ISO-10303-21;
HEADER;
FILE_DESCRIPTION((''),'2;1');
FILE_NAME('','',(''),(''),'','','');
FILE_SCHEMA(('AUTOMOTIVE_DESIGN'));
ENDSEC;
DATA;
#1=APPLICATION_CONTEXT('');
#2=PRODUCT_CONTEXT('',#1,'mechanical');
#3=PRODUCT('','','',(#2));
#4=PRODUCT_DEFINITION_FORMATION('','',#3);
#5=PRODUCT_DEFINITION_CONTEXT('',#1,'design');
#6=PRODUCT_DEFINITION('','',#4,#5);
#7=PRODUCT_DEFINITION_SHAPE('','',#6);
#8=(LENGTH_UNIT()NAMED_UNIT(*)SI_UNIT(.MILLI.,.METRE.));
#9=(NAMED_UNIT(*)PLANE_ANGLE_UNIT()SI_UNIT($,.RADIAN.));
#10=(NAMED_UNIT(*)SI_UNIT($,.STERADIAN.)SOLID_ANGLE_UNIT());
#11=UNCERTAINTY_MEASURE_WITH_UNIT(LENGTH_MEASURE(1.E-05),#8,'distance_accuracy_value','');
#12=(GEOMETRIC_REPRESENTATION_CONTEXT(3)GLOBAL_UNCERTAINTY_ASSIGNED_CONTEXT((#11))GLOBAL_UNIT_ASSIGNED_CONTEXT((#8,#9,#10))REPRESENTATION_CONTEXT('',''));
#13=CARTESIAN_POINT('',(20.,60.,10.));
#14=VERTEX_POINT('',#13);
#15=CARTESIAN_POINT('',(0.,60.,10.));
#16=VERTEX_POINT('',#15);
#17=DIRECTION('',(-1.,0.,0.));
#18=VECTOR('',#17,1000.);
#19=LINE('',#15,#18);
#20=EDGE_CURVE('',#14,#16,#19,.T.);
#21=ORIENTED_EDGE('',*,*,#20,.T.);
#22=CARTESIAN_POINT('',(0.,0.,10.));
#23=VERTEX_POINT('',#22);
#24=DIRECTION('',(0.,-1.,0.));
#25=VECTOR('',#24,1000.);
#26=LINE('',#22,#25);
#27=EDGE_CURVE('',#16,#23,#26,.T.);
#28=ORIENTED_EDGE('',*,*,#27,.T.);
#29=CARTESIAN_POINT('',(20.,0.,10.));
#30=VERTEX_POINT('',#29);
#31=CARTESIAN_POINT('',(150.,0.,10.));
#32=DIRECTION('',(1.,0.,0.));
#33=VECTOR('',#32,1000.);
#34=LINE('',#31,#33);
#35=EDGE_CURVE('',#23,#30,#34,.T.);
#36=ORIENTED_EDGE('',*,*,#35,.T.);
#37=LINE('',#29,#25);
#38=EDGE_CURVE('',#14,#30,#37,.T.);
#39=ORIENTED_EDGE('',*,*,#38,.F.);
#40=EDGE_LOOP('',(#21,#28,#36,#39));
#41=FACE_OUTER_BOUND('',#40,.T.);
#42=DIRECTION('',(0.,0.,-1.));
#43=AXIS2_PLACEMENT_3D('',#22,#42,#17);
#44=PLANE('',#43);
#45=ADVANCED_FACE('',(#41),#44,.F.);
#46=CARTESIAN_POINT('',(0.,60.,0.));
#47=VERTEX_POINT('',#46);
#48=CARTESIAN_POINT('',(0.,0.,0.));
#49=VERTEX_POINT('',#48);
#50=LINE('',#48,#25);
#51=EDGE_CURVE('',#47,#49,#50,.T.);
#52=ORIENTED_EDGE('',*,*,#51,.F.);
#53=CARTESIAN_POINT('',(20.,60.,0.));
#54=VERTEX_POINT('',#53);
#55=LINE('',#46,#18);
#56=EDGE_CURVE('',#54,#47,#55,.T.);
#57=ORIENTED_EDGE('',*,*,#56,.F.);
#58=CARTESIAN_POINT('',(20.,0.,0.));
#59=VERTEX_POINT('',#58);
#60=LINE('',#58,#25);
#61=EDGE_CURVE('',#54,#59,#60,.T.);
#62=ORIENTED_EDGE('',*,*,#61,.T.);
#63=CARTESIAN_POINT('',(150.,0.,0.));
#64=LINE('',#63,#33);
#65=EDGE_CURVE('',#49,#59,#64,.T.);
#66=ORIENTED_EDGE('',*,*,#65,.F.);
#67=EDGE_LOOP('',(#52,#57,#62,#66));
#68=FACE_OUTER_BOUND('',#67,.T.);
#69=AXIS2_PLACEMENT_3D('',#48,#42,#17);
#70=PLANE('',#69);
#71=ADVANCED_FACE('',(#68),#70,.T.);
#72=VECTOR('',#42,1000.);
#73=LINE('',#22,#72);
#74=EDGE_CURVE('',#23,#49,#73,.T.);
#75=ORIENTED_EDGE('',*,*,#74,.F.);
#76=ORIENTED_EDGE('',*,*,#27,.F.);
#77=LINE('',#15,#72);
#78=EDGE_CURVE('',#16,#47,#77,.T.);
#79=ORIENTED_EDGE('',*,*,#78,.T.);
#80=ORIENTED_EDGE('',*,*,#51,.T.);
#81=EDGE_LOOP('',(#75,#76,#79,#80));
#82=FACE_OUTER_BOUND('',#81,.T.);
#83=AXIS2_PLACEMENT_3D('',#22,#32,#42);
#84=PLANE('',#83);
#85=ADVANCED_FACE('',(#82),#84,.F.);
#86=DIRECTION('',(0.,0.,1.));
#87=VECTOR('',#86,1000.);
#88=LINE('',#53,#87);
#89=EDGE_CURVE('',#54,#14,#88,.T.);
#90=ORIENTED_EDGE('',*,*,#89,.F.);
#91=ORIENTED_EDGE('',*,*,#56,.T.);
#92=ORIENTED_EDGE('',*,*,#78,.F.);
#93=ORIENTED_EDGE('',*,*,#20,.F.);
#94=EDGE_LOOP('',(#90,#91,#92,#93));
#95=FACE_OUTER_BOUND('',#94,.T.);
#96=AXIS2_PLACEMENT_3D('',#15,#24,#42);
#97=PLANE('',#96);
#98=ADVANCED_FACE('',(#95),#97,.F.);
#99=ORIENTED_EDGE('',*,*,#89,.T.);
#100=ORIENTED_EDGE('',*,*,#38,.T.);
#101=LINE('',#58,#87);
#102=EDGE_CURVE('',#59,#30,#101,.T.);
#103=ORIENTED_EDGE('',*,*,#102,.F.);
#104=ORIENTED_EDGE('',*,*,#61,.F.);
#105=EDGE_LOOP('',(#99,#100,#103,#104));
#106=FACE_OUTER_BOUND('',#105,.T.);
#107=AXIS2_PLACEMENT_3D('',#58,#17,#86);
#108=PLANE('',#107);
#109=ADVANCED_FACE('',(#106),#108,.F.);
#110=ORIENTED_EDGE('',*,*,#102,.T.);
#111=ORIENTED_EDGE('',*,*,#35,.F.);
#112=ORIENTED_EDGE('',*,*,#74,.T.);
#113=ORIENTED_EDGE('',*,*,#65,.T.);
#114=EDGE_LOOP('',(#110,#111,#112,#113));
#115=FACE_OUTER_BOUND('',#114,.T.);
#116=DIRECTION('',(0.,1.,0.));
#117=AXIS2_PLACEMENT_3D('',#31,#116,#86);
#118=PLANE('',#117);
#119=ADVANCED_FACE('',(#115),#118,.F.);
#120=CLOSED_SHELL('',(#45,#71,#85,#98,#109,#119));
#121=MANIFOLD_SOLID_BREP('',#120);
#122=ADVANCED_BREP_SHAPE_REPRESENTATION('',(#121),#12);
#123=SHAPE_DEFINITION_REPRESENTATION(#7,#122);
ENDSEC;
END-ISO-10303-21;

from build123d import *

# Parameters (mm, degrees)
SKETCH_1_W          = 150
SKETCH_1_H          = 60
EXTRUDE_1_DEPTH     = 10
SKETCH_2_W          = 30
SKETCH_2_H          = 80
CUT_EXTRUDE_1_DEPTH = 80
SKETCH_3_W          = 50
SKETCH_3_H          = 60
CUT_EXTRUDE_3_DEPTH = 10


with BuildPart() as part:
    # 草图1 → 凸台-拉伸1 (new body)
    with BuildSketch(Plane.XY):
        with Locations((75, 30)):
            Rectangle(SKETCH_1_W, SKETCH_1_H)
    extrude(amount=EXTRUDE_1_DEPTH)

    # 草图2 → 切除-拉伸1 (cut)
    with BuildSketch(Plane(origin=(150, 0, 0), x_dir=(0, 0, -1), z_dir=(1, 0, 0))):
        with Locations((-5, 30)):
            Rectangle(SKETCH_2_W, SKETCH_2_H)
    extrude(amount=-CUT_EXTRUDE_1_DEPTH, mode=Mode.SUBTRACT)

    # 草图3 → 切除-拉伸3 (cut)
    with BuildSketch(Plane.XY.offset(10)):
        with Locations((45, 30)):
            Rectangle(SKETCH_3_W, SKETCH_3_H)
    extrude(amount=-CUT_EXTRUDE_3_DEPTH, mode=Mode.SUBTRACT)


solid = part.part
